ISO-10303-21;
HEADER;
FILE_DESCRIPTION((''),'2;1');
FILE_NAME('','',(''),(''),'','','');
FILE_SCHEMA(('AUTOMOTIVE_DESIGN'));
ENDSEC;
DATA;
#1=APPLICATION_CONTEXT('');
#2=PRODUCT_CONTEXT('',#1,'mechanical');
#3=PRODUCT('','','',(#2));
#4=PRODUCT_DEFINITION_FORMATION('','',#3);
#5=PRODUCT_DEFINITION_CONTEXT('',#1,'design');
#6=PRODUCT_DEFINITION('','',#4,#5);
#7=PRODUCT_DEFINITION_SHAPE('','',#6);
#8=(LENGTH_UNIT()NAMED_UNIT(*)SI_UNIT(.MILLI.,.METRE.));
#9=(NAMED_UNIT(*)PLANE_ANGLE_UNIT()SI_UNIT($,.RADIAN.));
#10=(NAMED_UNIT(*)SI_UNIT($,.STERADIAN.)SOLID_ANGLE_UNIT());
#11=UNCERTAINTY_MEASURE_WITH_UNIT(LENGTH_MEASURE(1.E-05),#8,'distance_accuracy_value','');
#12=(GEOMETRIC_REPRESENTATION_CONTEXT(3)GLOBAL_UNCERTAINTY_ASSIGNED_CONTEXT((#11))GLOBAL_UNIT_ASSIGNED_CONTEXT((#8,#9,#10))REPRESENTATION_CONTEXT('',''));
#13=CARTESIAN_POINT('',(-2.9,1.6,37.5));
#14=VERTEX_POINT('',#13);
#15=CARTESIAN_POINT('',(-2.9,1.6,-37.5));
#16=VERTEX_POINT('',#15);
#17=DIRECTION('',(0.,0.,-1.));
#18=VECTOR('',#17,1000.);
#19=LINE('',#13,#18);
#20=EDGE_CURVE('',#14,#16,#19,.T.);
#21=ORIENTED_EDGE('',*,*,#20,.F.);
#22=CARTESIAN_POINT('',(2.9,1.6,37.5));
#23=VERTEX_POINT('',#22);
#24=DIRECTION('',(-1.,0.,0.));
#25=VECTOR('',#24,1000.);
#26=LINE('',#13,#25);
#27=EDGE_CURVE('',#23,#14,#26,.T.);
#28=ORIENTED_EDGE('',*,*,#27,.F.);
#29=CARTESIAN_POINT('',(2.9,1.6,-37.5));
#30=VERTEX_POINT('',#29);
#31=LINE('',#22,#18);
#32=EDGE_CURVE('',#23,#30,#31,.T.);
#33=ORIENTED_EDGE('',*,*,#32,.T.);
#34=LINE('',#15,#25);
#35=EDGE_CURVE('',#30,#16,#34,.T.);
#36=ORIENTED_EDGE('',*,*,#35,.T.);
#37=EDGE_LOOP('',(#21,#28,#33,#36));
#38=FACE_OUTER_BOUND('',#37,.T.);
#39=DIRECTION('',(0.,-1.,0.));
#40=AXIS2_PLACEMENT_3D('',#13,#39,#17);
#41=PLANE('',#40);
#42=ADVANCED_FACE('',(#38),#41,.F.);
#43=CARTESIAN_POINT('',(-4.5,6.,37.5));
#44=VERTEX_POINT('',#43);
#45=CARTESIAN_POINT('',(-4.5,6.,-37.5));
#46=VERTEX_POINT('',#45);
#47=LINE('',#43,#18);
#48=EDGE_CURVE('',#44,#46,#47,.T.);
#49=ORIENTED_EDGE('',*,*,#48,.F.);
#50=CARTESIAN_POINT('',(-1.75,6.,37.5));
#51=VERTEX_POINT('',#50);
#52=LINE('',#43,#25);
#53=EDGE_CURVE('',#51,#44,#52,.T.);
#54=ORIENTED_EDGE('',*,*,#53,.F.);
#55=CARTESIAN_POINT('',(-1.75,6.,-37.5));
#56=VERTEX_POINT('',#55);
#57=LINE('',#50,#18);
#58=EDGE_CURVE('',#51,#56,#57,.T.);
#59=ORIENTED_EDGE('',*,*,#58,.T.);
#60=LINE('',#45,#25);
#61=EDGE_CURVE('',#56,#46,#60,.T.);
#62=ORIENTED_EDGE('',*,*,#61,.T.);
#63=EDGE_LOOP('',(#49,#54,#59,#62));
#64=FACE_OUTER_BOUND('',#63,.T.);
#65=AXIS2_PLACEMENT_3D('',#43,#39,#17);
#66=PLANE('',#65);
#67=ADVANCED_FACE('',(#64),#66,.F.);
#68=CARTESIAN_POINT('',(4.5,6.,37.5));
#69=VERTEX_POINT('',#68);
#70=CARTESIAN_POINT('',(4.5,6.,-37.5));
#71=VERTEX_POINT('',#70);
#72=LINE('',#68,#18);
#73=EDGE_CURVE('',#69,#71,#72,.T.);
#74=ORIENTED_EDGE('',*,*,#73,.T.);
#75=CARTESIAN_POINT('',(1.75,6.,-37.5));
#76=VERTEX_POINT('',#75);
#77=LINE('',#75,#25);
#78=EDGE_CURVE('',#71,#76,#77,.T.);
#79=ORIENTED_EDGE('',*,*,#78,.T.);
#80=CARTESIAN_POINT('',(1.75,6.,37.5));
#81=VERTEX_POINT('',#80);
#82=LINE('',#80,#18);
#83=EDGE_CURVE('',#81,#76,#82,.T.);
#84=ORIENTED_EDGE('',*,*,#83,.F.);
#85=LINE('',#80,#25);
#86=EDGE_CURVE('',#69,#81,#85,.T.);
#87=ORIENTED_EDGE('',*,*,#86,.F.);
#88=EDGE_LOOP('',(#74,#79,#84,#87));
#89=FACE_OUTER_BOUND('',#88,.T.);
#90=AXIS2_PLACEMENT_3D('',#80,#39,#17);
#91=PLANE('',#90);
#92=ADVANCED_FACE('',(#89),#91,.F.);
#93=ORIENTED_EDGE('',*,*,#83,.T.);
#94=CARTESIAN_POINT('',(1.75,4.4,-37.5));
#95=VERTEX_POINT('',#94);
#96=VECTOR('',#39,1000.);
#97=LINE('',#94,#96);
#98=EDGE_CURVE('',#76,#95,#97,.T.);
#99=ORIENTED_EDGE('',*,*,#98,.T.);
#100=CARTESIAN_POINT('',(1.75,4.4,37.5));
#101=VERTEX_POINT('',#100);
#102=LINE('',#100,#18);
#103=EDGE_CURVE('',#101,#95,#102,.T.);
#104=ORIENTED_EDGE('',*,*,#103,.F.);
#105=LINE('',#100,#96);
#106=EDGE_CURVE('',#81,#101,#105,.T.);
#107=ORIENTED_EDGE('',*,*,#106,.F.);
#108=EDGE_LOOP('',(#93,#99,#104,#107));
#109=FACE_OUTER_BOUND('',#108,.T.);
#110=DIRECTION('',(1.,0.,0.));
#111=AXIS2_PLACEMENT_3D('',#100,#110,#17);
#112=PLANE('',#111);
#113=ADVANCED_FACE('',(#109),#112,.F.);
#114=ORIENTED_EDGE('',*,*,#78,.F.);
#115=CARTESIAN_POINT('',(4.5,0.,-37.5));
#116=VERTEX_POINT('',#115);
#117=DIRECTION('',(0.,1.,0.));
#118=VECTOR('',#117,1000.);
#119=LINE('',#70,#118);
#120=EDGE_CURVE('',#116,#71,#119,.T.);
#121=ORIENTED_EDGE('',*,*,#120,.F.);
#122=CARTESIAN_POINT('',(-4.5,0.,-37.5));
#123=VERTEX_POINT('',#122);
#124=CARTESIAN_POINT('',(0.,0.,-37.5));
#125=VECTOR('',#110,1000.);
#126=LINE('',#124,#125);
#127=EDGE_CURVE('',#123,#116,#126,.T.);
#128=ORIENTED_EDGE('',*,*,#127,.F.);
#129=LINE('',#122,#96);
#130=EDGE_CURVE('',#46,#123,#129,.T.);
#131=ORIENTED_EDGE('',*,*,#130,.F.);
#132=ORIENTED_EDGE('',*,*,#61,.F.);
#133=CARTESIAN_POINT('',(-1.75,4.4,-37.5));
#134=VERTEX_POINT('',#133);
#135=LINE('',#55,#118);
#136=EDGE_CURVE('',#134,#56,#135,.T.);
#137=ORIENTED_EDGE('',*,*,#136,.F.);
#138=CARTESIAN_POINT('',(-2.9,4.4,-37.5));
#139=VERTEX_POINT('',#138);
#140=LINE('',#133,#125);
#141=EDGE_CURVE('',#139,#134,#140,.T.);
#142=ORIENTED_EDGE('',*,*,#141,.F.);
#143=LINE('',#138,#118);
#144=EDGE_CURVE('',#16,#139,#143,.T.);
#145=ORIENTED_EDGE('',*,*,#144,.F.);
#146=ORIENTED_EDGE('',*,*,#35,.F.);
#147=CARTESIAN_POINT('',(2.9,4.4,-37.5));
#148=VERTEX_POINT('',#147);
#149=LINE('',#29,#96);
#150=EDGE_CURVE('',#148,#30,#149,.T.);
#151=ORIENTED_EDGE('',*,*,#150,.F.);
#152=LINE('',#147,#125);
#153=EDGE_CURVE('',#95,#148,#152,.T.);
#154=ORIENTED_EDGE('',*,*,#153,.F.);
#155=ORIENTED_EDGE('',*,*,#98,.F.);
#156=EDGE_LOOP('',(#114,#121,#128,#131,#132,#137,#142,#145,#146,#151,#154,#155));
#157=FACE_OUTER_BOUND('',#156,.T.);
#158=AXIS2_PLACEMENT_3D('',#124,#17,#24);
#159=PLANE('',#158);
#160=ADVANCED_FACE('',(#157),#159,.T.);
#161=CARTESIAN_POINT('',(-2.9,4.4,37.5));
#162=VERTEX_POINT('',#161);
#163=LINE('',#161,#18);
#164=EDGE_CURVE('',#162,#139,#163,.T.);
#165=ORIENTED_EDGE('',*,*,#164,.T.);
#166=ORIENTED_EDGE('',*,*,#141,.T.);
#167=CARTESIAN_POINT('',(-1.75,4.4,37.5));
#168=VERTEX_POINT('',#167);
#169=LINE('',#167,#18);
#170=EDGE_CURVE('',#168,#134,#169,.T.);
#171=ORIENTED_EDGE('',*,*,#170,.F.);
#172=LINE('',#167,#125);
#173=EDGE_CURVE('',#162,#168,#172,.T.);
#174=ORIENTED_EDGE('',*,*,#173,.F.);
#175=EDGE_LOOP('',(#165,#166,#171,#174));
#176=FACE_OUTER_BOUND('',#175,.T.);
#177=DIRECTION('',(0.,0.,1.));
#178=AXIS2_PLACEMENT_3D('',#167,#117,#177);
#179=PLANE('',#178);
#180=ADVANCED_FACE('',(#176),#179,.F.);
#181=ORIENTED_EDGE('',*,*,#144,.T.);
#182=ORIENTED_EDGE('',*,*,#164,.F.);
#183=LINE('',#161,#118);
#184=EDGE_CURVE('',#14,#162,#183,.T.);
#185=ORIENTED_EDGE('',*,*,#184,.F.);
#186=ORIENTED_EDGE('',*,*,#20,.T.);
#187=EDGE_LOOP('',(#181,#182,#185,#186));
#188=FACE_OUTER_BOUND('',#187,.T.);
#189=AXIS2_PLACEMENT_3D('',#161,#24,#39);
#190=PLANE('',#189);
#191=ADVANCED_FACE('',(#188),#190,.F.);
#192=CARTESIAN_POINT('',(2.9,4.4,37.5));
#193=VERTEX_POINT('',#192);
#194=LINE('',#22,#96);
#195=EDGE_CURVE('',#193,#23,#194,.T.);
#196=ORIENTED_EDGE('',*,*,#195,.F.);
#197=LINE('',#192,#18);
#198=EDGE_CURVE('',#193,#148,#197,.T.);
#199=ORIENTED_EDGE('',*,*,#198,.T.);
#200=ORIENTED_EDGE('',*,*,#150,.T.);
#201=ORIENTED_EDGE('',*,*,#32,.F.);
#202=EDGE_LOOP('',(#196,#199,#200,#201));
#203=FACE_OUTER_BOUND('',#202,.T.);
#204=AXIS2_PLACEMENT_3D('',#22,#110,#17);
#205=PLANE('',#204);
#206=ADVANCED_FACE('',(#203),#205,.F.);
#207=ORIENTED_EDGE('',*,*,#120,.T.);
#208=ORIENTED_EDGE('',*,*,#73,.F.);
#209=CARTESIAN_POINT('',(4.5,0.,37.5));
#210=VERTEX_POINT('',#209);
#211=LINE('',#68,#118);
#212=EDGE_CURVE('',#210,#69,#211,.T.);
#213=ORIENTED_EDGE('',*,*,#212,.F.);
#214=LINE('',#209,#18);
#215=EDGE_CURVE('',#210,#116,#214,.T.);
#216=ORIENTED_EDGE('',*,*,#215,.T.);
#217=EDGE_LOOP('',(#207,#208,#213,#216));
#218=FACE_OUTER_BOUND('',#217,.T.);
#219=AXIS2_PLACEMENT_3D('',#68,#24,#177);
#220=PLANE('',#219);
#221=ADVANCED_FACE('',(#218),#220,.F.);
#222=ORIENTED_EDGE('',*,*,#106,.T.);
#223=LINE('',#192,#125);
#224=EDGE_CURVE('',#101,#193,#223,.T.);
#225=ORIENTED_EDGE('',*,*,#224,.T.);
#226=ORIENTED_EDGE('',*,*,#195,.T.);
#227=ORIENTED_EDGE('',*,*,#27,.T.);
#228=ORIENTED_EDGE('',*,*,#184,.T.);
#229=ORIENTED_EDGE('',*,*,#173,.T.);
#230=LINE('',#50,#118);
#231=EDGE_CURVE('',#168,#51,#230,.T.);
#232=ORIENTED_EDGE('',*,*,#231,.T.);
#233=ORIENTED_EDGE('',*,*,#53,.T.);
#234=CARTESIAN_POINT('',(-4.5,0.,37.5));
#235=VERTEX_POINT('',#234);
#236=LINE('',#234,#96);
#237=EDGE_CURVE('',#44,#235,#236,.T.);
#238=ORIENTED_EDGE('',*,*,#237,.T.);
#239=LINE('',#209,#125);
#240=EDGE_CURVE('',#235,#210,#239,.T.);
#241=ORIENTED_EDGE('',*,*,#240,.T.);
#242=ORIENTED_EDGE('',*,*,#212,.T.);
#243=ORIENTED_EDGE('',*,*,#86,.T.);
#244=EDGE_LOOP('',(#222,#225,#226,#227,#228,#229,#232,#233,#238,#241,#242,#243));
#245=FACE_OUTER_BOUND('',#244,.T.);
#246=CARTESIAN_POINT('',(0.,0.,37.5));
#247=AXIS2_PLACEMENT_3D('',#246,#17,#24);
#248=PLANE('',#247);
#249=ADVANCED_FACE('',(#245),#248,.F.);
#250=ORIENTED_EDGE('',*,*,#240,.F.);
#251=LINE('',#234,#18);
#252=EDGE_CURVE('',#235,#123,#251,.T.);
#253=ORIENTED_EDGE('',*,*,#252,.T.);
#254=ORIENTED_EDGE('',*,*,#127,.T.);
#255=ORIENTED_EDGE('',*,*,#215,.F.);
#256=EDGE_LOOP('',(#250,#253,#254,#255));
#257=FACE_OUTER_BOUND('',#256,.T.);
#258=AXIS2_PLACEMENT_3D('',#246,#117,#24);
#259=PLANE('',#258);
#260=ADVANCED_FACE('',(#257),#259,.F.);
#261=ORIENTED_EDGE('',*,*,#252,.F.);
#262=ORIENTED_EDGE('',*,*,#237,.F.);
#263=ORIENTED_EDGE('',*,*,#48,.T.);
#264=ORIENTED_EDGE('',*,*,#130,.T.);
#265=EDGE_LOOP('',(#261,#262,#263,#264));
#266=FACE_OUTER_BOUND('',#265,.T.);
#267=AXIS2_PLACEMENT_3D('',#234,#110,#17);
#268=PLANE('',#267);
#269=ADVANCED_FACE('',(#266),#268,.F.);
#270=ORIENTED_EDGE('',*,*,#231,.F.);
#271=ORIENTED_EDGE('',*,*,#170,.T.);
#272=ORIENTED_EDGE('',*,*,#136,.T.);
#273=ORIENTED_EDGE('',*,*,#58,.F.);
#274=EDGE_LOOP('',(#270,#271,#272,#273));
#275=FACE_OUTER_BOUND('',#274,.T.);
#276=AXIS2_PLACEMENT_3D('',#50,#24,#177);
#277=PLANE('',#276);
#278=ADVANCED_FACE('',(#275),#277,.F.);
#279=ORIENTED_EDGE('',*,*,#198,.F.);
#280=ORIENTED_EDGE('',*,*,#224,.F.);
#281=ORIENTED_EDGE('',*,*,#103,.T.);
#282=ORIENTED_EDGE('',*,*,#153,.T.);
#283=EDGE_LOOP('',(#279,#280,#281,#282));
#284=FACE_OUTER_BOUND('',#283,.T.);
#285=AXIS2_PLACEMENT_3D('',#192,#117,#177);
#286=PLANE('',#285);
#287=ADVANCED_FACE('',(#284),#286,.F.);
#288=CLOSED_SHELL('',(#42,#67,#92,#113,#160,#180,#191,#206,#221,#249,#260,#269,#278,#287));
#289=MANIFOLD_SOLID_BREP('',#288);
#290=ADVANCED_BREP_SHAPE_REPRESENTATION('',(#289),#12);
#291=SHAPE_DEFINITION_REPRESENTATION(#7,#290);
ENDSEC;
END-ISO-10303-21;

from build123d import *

# Parameters (mm, degrees)
EXTRUDE_1_DEPTH = 37.5


with BuildPart() as part:
    # 草图1 → 凸台-拉伸1 (new, symmetric)
    with BuildSketch(Plane.XY):
        Polygon((0, 0), (-4.5, 0), (-4.5, 6), (-1.75, 6), (-1.75, 4.4), (-2.9, 4.4), (-2.9, 1.6), (2.9, 1.6), (2.9, 4.4), (1.75, 4.4), (1.75, 6), (4.5, 6), (4.5, 0), align=None)
    extrude(amount=EXTRUDE_1_DEPTH, both=True)


solid = part.part
